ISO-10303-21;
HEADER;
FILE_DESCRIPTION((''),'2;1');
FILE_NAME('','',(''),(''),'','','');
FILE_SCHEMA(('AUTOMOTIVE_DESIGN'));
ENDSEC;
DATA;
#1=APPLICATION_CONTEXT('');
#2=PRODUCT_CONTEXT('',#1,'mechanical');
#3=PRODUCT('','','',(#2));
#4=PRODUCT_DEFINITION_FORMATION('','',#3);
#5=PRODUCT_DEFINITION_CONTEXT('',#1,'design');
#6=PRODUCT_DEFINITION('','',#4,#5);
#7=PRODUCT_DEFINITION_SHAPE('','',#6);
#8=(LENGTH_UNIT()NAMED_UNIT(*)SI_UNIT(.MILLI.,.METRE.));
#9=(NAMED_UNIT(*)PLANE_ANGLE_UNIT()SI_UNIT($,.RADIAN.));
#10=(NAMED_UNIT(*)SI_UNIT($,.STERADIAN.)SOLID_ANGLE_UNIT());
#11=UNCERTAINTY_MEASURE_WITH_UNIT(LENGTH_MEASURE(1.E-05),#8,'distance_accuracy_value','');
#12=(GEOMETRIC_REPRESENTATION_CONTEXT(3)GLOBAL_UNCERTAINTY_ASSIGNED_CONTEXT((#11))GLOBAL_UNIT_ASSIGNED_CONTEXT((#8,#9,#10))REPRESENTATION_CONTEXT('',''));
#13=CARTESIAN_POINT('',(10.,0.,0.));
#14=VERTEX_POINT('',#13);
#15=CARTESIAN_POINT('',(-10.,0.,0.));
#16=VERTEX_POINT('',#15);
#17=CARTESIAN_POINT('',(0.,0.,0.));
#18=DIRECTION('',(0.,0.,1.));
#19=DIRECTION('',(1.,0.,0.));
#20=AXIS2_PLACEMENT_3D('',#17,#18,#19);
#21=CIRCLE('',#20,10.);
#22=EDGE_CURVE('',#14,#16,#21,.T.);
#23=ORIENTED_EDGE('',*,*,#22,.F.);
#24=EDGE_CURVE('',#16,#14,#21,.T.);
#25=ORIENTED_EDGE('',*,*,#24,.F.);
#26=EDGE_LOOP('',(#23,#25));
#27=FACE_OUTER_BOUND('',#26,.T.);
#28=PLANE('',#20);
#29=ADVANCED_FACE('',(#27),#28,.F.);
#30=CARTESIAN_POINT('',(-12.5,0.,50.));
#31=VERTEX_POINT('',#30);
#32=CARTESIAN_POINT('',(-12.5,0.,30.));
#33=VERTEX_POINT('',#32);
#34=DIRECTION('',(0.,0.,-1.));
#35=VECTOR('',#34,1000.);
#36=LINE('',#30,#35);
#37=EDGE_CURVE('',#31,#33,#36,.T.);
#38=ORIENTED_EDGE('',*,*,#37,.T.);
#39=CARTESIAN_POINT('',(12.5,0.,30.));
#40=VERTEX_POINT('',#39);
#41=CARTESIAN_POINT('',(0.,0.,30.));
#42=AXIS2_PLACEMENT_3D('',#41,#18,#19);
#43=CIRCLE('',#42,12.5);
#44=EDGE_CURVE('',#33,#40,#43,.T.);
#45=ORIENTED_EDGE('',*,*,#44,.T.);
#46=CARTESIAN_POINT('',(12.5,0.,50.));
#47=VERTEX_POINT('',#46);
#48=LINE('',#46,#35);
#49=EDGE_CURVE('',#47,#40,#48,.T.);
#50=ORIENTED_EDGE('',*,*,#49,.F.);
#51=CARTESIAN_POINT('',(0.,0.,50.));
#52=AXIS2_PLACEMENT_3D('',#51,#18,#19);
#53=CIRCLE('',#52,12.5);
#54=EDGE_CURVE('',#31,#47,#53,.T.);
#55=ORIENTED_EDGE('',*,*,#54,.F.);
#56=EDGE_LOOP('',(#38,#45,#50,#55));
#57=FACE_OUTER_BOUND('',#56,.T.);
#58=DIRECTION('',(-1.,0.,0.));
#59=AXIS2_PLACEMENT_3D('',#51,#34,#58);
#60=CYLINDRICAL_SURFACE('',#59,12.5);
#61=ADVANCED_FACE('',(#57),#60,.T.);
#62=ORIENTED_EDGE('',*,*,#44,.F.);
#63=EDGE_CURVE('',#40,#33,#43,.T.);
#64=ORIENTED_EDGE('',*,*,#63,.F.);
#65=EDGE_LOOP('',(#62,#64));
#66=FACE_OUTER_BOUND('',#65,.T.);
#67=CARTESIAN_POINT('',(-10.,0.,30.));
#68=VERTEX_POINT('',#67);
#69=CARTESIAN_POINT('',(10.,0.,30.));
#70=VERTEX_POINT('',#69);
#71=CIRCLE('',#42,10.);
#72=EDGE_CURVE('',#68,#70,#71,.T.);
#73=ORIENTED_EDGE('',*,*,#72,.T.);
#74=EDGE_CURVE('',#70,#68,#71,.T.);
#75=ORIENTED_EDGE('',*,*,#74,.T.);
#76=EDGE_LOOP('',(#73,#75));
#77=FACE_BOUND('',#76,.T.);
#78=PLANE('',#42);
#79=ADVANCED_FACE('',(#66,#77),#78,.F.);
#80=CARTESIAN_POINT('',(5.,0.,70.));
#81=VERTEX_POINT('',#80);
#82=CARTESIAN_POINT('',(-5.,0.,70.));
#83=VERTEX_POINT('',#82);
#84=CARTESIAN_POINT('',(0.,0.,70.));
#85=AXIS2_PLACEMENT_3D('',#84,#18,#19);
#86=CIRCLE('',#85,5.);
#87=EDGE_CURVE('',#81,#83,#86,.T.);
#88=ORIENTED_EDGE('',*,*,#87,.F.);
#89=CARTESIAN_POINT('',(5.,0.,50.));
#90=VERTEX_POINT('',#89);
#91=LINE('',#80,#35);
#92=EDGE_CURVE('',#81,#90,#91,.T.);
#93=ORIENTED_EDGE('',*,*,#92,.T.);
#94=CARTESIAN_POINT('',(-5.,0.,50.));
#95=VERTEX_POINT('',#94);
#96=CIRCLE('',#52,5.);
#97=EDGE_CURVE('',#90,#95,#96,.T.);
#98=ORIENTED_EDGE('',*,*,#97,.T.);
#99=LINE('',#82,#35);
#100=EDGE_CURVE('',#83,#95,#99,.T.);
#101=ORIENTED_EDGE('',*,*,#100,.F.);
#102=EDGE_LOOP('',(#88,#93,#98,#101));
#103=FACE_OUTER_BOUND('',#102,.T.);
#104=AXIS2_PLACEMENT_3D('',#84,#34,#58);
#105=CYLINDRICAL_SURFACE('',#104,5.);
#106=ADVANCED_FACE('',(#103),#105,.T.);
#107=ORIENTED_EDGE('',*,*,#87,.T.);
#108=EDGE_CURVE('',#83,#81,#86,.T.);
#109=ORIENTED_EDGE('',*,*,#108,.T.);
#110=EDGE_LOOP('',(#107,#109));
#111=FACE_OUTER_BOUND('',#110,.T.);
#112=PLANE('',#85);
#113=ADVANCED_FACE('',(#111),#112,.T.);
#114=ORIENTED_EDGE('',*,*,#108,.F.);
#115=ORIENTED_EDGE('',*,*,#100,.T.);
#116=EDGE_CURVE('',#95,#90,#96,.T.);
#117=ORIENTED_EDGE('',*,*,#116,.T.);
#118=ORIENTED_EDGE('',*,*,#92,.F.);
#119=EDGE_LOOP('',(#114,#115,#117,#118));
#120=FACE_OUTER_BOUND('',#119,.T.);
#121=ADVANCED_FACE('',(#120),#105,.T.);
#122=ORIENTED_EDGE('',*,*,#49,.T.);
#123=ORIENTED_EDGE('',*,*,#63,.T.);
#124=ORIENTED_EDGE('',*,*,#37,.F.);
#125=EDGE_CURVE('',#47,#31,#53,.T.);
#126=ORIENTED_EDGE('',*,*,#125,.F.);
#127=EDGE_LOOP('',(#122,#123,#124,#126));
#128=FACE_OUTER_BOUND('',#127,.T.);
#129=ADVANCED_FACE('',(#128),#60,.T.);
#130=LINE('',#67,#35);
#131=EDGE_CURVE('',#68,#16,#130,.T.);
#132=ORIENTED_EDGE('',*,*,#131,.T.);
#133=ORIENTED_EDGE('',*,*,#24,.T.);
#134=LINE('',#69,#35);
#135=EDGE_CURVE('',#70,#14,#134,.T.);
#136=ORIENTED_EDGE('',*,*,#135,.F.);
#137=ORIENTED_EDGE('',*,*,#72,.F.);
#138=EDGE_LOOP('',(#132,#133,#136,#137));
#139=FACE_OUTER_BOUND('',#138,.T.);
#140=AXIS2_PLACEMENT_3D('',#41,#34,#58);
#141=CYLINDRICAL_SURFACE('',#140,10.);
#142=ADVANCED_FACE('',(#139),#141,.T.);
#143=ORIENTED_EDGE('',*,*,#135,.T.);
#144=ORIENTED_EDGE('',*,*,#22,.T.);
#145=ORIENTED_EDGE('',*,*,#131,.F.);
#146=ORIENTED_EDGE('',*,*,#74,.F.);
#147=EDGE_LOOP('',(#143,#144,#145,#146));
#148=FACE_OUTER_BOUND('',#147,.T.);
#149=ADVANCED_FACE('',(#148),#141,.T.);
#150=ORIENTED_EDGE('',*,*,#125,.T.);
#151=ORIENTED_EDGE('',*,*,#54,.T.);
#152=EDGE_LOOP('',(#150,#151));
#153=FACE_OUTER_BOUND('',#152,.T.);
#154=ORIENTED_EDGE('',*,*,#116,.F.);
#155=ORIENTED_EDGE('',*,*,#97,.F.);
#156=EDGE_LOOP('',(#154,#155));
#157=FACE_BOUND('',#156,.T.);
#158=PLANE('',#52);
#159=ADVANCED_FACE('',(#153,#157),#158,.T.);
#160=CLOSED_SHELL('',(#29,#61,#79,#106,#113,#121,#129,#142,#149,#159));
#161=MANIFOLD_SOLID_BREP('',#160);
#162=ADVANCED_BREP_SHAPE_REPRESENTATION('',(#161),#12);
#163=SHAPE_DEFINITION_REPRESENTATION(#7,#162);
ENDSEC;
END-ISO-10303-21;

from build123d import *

# Parameters (mm, degrees)
SKETCH1_R           = 10
BOSS_EXTRUDE1_DEPTH = 30
SKETCH2_R           = 12.5
BOSS_EXTRUDE2_DEPTH = 20
SKETCH3_R           = 5
BOSS_EXTRUDE3_DEPTH = 20


with BuildPart() as part:
    # Sketch1 → Boss-Extrude1 (new body)
    with BuildSketch(Plane.XY):
        Circle(SKETCH1_R)
    extrude(amount=BOSS_EXTRUDE1_DEPTH)

    # Sketch2 → Boss-Extrude2 (add)
    with BuildSketch(Plane.XY.offset(30)):
        Circle(SKETCH2_R)
    extrude(amount=BOSS_EXTRUDE2_DEPTH)

    # Sketch3 → Boss-Extrude3 (add)
    with BuildSketch(Plane.XY.offset(50)):
        Circle(SKETCH3_R)
    extrude(amount=BOSS_EXTRUDE3_DEPTH)


solid = part.part
